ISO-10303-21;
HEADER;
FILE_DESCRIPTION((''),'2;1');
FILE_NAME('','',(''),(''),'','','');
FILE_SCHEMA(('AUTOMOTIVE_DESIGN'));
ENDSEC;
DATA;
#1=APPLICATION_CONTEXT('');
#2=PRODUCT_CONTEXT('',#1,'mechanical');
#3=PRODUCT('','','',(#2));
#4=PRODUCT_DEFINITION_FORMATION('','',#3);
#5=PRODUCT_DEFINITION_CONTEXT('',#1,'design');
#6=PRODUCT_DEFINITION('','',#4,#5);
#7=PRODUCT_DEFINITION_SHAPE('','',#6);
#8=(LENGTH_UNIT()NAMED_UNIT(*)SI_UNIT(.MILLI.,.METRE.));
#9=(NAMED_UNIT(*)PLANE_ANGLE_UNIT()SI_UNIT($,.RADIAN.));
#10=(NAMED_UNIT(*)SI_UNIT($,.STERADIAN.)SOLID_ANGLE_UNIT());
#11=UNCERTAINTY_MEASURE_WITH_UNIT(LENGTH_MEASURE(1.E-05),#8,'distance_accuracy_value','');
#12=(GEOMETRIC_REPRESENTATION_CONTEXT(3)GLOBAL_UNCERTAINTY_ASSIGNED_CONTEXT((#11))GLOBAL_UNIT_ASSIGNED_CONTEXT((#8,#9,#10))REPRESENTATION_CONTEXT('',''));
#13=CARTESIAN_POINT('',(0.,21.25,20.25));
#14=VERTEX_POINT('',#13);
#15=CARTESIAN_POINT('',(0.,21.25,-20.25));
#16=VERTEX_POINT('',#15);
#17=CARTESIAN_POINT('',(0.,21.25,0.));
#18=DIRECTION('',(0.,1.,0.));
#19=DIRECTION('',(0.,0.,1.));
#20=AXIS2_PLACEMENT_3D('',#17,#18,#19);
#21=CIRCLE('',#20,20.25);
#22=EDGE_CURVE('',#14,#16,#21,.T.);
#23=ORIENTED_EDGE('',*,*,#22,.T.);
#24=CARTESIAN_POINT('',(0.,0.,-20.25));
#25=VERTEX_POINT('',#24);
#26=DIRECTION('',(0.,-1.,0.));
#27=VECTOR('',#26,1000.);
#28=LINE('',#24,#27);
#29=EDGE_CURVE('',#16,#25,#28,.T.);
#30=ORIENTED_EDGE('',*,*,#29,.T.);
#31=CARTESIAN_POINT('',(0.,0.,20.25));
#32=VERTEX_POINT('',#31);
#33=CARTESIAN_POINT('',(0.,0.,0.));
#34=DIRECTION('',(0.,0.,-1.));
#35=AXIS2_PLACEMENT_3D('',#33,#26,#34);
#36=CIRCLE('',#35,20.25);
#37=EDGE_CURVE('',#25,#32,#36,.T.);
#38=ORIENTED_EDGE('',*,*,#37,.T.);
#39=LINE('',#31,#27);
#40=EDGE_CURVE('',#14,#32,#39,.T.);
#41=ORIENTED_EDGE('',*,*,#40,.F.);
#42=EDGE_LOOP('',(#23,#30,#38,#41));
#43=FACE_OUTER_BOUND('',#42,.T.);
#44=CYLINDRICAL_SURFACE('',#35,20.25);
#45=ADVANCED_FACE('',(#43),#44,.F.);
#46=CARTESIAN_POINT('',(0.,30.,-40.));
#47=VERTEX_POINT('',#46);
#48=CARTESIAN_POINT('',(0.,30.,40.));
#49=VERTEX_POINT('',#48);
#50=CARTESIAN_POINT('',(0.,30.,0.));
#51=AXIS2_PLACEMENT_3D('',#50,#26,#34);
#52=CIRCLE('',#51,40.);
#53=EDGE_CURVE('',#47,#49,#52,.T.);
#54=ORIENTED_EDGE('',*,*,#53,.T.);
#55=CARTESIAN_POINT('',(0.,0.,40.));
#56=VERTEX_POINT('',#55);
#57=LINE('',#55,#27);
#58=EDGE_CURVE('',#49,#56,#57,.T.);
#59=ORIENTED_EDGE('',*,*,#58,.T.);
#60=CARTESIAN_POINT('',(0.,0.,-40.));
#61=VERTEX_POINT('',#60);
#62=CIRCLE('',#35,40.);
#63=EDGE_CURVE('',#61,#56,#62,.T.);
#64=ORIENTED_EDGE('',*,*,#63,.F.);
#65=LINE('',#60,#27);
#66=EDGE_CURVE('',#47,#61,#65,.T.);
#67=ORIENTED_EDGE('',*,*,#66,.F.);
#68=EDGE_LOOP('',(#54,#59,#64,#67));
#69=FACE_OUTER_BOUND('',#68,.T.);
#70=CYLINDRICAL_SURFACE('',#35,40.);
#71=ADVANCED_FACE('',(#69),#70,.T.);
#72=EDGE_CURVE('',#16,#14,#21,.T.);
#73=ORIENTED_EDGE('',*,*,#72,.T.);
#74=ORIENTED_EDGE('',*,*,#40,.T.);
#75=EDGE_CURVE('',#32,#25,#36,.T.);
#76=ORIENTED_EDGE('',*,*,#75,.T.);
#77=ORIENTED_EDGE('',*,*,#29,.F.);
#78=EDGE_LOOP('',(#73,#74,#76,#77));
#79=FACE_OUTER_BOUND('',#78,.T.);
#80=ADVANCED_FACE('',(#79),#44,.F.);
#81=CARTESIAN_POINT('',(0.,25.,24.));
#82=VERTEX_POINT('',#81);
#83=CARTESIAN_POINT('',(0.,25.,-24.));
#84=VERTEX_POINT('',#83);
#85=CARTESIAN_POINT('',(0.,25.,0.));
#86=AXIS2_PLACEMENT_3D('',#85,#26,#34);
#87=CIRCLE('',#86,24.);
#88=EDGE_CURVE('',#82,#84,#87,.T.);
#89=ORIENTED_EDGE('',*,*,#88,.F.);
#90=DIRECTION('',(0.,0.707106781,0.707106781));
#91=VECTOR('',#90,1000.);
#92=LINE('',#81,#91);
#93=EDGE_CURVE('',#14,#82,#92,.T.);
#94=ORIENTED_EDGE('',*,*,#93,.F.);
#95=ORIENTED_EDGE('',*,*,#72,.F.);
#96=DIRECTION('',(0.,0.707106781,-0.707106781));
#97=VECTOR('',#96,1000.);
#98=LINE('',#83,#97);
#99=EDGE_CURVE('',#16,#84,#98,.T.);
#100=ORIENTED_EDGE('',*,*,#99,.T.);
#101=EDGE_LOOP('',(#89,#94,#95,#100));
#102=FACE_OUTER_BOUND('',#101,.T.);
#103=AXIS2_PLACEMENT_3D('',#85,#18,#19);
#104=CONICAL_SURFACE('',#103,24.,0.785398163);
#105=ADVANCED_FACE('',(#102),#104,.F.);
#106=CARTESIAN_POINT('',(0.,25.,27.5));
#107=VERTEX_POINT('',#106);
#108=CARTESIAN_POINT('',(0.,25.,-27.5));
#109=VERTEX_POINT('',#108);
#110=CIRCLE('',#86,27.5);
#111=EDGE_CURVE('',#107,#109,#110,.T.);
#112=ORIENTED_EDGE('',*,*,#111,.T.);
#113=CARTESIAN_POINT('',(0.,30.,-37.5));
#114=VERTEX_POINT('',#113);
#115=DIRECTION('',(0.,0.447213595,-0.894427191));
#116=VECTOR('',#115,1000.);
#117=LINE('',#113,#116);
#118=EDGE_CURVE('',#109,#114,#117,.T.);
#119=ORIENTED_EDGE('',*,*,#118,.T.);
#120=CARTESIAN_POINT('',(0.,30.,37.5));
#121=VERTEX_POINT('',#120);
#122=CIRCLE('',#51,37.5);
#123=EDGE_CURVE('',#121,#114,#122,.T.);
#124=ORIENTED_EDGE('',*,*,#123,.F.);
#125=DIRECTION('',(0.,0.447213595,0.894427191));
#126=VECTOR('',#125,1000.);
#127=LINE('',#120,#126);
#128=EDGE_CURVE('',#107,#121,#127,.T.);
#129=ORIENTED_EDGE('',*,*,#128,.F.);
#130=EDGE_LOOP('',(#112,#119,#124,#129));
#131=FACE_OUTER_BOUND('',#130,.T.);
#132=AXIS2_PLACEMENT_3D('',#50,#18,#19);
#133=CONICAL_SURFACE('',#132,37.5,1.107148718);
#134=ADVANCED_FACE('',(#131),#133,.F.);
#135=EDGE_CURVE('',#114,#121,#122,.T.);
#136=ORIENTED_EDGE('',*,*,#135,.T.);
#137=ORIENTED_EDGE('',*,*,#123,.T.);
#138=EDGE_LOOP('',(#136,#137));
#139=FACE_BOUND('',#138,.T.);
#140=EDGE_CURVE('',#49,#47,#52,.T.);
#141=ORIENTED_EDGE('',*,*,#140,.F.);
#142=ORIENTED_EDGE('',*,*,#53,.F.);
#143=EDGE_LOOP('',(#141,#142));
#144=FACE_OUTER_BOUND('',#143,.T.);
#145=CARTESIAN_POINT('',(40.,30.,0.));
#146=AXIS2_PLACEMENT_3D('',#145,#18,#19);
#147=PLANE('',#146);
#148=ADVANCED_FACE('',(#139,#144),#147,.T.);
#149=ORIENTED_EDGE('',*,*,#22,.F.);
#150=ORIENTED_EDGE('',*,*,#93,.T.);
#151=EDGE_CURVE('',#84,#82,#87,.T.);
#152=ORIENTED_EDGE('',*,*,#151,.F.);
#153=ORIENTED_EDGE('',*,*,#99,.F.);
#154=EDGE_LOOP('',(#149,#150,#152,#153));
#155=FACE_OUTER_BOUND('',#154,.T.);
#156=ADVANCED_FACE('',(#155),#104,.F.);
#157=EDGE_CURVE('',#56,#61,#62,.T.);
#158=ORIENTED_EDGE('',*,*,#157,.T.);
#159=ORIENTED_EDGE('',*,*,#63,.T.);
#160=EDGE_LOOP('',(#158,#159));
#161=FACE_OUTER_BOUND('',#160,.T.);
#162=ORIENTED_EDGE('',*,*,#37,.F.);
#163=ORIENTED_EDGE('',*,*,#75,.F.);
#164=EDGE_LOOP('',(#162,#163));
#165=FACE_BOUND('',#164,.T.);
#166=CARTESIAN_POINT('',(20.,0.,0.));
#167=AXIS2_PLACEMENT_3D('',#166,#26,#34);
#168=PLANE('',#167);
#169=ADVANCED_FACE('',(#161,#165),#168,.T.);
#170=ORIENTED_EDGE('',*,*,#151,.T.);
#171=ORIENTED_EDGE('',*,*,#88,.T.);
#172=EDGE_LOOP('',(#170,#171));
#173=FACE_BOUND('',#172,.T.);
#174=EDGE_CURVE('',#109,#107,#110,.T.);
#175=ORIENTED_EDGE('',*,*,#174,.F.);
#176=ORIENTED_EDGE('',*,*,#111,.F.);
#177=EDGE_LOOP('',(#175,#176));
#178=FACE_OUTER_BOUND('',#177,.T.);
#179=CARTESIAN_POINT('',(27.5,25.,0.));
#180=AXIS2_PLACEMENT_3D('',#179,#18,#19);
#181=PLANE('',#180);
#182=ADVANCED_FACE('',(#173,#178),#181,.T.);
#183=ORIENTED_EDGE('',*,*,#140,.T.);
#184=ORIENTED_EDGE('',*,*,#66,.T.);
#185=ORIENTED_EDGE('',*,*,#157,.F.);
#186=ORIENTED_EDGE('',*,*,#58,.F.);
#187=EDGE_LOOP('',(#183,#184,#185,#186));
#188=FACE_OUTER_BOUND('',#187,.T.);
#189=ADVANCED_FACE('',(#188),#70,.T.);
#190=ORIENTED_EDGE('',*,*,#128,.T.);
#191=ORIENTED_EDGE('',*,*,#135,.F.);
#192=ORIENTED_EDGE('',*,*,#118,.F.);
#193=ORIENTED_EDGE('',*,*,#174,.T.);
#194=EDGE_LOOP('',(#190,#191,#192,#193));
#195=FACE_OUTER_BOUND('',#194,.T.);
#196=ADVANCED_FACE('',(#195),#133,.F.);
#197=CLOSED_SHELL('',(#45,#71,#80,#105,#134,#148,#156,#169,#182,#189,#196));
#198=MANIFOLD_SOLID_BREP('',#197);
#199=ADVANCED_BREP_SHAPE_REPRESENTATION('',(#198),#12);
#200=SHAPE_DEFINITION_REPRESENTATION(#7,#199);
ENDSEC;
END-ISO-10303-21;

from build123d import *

# Parameters (mm, degrees)
M42X1_5_TAPPED_HOLE1_D     = 40.5
M42X1_5_TAPPED_HOLE1_DEPTH = 88.5
M42X1_5_TAPPED_HOLE1_TIP   = 12.167427535


with BuildPart() as part:
    # Sketch1 → Revolve1 (revolve)
    with BuildSketch(Plane.XY, mode=Mode.PRIVATE) as revolve1_sk:
        Polygon((20, 0), (40, 0), (40, 30), (37.5, 30), (27.5, 25), (24, 25), (20, 21), align=None)
    revolve(revolve1_sk.sketch.rotate(Axis((0, 0, 0), (0, 1, 0)), 90), axis=Axis((0, 0, 0), (0, 1, 0)))

    # M42X1.5 Tapped Hole1
    with Locations(Plane(origin=(0, 0, 0), x_dir=(-1, 0, 0), z_dir=(0, -1, 0))):
        with Locations((0, 0)):
            Hole(M42X1_5_TAPPED_HOLE1_D / 2, depth=M42X1_5_TAPPED_HOLE1_DEPTH)
            with Locations((0, 0, -(M42X1_5_TAPPED_HOLE1_DEPTH + M42X1_5_TAPPED_HOLE1_TIP / 2))):  # 118° drill point
                Cone(0, M42X1_5_TAPPED_HOLE1_D / 2, M42X1_5_TAPPED_HOLE1_TIP, mode=Mode.SUBTRACT)


solid = part.part
